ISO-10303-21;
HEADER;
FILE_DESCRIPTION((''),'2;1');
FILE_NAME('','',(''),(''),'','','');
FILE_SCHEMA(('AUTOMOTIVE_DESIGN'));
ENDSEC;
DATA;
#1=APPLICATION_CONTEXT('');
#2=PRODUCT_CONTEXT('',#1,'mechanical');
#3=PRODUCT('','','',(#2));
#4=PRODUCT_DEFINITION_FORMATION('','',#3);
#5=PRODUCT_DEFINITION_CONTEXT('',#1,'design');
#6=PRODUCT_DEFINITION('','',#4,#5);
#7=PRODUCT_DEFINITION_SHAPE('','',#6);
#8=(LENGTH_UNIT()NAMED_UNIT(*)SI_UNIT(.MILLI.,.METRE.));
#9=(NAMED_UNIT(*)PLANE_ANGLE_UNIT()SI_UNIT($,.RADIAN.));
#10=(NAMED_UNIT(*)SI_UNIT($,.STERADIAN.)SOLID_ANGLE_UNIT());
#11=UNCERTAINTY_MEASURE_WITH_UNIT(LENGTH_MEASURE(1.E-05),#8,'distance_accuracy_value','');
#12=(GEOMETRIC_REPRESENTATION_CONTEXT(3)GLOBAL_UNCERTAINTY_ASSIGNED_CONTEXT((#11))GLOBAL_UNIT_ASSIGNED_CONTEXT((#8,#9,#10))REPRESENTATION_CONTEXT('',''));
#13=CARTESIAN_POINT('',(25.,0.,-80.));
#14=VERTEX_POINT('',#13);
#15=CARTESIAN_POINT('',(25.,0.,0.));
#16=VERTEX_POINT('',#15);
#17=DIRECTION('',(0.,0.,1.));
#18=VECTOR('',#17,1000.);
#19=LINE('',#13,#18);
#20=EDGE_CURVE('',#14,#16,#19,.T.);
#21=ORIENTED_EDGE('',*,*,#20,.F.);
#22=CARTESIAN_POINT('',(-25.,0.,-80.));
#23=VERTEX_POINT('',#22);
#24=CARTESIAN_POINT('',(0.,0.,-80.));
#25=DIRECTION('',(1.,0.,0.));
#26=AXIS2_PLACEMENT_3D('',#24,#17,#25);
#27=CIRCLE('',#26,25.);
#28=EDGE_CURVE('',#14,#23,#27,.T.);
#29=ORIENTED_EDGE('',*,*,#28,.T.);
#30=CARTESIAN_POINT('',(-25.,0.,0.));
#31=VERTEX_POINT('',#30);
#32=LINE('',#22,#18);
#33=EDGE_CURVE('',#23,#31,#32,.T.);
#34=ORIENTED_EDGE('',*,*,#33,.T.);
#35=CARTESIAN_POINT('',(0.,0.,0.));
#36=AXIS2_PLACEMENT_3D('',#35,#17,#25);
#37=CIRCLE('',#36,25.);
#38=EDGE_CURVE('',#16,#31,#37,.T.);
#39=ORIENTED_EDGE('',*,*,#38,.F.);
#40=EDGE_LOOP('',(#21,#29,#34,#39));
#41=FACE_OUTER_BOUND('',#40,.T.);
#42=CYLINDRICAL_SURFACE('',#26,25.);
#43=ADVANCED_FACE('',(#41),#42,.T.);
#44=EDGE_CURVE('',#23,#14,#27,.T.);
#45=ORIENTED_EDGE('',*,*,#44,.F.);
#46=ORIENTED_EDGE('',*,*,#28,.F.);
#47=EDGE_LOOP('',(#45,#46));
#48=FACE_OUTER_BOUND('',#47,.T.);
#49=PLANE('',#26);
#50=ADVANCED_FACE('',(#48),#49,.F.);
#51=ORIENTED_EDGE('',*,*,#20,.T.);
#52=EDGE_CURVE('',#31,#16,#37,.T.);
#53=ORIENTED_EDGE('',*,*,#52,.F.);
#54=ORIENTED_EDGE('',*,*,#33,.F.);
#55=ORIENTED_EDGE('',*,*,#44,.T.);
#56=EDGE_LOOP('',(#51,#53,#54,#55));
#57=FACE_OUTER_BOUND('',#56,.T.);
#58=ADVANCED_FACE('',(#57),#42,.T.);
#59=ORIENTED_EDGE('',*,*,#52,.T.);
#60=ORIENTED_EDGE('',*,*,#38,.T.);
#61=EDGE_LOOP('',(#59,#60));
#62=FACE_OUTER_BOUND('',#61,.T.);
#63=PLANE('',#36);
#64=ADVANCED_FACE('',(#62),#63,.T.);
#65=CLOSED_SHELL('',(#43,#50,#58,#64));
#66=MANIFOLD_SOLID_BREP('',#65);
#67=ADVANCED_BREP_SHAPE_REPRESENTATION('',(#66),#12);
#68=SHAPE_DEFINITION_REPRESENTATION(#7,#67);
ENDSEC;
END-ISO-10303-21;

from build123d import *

# Parameters (mm, degrees)
SKETCH_1_R      = 25
EXTRUDE_1_DEPTH = 80


with BuildPart() as part:
    # 草图1 → 凸台-拉伸1 (new body)
    with BuildSketch(Plane.XY):
        Circle(SKETCH_1_R)
    extrude(amount=-EXTRUDE_1_DEPTH)


solid = part.part
